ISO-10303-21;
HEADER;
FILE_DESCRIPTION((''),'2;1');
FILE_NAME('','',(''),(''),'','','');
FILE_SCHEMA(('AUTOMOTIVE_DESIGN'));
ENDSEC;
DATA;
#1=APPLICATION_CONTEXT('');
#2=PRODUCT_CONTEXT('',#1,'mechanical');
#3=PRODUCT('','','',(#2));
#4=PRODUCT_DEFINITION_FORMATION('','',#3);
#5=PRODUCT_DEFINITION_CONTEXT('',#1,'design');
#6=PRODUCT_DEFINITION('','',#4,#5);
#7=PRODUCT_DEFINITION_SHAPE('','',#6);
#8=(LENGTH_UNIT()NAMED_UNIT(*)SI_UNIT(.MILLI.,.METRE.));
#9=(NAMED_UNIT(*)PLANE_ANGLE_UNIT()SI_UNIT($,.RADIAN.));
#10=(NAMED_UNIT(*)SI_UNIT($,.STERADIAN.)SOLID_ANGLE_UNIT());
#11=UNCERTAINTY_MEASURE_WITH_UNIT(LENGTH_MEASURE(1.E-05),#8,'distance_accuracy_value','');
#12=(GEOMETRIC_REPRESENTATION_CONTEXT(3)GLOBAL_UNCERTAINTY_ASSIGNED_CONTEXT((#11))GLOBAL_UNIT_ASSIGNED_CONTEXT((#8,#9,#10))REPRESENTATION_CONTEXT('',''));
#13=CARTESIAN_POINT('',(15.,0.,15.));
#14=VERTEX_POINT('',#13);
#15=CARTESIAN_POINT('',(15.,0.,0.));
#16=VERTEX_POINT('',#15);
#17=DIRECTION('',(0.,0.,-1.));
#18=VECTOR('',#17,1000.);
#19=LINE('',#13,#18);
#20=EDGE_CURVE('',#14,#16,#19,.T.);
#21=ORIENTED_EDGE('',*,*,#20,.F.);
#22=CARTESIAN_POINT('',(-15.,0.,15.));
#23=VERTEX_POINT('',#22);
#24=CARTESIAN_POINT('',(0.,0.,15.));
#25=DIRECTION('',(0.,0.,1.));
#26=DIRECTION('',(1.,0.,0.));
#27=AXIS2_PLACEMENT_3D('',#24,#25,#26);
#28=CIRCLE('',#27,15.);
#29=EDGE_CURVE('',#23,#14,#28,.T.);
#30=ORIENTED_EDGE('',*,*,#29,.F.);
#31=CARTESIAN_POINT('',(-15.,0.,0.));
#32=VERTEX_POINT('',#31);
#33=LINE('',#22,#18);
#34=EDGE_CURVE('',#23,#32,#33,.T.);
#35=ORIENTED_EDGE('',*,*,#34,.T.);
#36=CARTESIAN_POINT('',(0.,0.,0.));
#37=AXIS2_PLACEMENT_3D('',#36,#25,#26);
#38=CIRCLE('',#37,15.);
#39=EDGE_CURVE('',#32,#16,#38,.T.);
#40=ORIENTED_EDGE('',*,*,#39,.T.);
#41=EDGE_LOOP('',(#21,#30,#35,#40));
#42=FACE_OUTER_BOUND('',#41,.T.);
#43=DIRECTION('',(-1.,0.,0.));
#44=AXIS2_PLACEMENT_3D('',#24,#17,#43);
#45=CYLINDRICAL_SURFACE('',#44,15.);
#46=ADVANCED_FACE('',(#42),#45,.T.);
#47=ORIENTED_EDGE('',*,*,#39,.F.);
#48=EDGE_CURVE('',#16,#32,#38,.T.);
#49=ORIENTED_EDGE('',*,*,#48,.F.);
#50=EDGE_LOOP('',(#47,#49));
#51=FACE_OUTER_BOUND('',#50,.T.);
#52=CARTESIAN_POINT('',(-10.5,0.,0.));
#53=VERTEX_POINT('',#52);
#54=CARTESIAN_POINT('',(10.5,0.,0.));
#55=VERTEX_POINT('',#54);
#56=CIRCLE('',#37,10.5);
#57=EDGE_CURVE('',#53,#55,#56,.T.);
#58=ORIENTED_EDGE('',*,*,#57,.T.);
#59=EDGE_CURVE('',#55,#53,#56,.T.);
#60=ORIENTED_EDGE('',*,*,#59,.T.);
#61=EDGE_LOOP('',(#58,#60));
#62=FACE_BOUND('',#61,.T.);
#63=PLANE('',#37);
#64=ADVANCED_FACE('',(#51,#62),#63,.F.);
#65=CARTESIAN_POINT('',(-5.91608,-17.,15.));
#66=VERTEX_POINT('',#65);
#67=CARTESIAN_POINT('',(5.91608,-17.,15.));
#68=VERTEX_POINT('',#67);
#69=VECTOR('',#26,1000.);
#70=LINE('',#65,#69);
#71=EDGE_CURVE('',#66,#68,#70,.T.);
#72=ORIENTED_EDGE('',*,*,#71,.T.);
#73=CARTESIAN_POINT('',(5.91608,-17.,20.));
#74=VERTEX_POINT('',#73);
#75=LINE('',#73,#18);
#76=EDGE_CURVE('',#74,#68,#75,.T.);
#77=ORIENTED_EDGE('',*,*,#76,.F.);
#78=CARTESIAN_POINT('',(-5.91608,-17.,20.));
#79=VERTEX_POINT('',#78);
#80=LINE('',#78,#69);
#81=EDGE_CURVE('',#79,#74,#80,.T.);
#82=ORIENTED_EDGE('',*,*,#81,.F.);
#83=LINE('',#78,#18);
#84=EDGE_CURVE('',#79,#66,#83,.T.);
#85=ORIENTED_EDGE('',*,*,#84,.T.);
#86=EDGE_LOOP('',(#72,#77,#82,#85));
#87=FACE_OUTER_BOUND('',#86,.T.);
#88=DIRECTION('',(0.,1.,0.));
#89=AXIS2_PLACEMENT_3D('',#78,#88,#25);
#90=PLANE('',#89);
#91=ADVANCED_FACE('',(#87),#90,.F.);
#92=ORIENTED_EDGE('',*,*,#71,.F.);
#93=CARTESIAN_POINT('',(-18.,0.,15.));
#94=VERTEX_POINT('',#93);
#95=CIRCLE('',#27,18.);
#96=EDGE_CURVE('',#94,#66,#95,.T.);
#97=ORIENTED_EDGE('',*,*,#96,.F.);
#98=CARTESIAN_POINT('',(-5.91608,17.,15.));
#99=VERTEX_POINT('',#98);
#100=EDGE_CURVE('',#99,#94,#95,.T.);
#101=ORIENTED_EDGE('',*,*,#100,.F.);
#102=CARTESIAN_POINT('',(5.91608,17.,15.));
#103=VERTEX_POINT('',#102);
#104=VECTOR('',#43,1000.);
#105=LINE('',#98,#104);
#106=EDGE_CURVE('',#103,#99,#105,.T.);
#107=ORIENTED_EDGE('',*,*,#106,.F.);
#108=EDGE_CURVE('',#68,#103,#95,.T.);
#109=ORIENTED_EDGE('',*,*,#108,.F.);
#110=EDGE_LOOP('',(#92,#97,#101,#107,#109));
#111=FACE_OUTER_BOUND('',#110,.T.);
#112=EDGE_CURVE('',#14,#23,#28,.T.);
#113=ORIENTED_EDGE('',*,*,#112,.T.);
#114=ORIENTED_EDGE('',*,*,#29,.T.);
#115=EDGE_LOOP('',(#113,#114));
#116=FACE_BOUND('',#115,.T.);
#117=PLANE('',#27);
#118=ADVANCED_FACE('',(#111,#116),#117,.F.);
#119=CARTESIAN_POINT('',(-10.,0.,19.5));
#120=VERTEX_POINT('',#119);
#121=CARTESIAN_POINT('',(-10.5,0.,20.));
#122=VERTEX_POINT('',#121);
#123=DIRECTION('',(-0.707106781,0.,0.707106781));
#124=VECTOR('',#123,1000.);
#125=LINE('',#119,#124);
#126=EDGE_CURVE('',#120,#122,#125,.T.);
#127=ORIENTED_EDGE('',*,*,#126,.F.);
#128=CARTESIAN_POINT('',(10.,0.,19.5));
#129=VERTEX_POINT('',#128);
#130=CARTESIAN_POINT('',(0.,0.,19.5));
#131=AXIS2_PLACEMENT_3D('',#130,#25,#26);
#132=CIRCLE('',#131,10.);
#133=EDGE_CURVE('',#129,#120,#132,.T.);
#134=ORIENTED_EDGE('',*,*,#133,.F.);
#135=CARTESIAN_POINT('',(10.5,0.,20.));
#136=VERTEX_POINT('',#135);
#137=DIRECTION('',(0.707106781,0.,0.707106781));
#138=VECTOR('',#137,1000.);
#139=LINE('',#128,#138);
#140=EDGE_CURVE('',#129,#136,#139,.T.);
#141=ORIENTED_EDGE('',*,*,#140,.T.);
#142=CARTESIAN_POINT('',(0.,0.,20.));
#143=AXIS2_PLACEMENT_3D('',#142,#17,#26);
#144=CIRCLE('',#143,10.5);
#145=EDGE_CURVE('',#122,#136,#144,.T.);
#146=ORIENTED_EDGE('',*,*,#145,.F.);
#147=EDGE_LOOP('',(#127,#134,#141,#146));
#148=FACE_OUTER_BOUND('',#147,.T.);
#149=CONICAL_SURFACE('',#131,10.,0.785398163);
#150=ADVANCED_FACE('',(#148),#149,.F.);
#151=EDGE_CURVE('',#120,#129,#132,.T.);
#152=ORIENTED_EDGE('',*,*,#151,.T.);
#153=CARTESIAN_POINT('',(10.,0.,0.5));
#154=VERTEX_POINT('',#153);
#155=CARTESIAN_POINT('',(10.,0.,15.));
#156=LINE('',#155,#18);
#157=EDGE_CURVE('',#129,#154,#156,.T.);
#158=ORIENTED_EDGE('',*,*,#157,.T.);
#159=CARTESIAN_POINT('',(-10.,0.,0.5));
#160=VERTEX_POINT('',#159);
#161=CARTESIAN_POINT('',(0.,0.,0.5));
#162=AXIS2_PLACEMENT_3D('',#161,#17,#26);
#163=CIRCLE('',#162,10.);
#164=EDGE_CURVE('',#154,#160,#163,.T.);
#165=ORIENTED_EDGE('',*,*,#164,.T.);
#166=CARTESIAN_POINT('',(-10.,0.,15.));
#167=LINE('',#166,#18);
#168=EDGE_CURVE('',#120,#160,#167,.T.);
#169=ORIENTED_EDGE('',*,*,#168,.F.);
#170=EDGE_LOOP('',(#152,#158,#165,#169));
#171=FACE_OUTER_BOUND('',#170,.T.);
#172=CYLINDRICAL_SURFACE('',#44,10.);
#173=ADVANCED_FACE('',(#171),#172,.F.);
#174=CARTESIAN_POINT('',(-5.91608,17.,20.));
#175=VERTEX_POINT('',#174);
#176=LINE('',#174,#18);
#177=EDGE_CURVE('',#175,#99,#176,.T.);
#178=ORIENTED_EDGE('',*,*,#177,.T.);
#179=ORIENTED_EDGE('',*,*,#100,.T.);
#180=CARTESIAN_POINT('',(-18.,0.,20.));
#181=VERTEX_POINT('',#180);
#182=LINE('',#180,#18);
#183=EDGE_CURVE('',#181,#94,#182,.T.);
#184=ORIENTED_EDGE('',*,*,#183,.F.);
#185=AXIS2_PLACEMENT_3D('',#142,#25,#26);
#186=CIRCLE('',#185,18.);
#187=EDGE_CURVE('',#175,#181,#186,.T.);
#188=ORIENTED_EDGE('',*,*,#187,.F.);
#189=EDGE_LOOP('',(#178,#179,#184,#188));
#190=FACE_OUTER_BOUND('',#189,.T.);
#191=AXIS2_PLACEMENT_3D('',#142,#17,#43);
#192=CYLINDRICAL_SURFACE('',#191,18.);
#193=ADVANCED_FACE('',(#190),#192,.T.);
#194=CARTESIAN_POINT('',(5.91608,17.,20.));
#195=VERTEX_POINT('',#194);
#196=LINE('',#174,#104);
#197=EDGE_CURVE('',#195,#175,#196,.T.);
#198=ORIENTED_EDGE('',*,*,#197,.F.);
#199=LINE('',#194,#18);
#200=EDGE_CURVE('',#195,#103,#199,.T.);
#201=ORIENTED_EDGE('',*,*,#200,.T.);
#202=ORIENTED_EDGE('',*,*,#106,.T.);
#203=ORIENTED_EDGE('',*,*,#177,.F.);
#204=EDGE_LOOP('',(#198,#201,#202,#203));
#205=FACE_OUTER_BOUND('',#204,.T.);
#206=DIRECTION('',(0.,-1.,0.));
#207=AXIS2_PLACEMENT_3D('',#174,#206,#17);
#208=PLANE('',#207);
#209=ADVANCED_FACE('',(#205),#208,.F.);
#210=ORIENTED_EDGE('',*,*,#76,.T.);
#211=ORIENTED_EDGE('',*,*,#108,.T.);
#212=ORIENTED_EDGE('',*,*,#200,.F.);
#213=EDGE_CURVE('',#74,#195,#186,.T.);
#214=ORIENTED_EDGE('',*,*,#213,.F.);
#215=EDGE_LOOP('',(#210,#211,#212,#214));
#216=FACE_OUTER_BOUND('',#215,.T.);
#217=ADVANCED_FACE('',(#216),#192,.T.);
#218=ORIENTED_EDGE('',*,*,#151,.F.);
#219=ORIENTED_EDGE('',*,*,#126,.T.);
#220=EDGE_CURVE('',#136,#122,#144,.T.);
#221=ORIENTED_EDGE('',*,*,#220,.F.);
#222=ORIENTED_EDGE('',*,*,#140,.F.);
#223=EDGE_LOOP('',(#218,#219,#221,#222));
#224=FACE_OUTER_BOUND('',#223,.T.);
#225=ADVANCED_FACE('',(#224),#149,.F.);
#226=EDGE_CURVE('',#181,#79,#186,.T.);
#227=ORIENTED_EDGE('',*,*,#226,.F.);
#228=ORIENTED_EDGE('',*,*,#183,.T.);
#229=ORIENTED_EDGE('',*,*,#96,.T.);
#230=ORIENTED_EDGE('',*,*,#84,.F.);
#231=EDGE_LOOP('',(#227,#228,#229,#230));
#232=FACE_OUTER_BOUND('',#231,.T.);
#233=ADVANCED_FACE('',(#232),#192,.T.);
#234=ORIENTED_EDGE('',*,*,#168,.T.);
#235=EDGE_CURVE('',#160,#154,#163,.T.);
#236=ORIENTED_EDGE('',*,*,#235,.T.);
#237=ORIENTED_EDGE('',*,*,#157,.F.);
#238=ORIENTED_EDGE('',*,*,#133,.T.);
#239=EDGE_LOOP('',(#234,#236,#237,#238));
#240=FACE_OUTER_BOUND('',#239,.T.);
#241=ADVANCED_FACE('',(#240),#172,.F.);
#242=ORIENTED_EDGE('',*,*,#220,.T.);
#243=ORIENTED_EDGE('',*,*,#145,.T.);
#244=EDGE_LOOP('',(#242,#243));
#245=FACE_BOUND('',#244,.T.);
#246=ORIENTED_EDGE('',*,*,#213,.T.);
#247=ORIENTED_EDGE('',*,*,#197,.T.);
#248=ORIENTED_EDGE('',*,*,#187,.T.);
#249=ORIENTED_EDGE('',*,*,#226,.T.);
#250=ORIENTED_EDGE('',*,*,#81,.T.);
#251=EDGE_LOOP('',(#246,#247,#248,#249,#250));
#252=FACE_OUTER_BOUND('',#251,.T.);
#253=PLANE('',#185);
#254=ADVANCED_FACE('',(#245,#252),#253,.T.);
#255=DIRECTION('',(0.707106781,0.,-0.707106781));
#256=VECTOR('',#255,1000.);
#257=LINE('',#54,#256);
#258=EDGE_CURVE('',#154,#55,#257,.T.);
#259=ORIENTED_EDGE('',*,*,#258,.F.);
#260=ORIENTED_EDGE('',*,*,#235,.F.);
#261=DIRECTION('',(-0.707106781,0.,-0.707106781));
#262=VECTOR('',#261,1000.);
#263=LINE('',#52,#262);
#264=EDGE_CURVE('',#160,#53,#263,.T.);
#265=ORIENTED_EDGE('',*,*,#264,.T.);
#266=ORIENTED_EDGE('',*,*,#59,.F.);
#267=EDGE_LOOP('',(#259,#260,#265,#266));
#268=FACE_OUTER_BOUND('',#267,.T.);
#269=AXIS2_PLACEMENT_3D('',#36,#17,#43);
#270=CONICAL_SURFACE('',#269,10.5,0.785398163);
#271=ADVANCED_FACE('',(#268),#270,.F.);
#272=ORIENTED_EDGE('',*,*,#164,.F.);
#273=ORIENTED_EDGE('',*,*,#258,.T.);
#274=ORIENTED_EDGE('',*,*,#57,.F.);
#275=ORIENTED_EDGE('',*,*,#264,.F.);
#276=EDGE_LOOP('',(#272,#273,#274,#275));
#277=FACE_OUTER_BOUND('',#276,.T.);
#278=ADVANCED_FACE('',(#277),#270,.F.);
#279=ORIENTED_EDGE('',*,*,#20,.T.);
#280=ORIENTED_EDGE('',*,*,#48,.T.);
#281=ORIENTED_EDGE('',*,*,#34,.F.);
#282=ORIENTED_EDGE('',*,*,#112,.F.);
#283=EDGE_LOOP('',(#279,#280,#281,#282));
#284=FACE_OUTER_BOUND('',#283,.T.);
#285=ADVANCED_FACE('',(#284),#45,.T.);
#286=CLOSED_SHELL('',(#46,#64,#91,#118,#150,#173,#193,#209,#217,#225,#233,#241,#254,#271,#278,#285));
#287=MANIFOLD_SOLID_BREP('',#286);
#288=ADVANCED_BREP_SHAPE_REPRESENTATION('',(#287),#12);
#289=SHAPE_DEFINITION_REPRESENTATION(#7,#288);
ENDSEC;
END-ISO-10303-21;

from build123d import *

# Parameters (mm, degrees)
SKETCH1_R           = 15
SKETCH1_R_2         = 10
BOSS_EXTRUDE1_DEPTH = 15
SKETCH2_R           = 10
BOSS_EXTRUDE2_DEPTH = 5
CHAMFER1_SIZE       = 0.5


with BuildPart() as part:
    # Sketch1 → Boss-Extrude1 (new body)
    with BuildSketch(Plane.XY):
        Circle(SKETCH1_R)
        Circle(SKETCH1_R_2, mode=Mode.SUBTRACT)
    extrude(amount=BOSS_EXTRUDE1_DEPTH)

    # Sketch2 → Boss-Extrude2 (add)
    with BuildSketch(Plane.XY.offset(15)):
        with BuildLine():
            Line((-5.916079783, 17), (5.916079783, 17))
            ThreePointArc((5.916079783, 17), (18, 0), (5.916079783, -17))
            Line((5.916079783, -17), (-5.916079783, -17))
            ThreePointArc((-5.916079783, -17), (-18, 0), (-5.916079783, 17))
        make_face()
        Circle(SKETCH2_R, mode=Mode.SUBTRACT)
    extrude(amount=BOSS_EXTRUDE2_DEPTH)

    # Chamfer1
    chamfer1_edges = [part.edges().sort_by_distance(p)[0] for p in [
        (-10, 0, 20),
        (-10, 0, 0),
    ]]
    chamfer(chamfer1_edges, length=CHAMFER1_SIZE)


solid = part.part
